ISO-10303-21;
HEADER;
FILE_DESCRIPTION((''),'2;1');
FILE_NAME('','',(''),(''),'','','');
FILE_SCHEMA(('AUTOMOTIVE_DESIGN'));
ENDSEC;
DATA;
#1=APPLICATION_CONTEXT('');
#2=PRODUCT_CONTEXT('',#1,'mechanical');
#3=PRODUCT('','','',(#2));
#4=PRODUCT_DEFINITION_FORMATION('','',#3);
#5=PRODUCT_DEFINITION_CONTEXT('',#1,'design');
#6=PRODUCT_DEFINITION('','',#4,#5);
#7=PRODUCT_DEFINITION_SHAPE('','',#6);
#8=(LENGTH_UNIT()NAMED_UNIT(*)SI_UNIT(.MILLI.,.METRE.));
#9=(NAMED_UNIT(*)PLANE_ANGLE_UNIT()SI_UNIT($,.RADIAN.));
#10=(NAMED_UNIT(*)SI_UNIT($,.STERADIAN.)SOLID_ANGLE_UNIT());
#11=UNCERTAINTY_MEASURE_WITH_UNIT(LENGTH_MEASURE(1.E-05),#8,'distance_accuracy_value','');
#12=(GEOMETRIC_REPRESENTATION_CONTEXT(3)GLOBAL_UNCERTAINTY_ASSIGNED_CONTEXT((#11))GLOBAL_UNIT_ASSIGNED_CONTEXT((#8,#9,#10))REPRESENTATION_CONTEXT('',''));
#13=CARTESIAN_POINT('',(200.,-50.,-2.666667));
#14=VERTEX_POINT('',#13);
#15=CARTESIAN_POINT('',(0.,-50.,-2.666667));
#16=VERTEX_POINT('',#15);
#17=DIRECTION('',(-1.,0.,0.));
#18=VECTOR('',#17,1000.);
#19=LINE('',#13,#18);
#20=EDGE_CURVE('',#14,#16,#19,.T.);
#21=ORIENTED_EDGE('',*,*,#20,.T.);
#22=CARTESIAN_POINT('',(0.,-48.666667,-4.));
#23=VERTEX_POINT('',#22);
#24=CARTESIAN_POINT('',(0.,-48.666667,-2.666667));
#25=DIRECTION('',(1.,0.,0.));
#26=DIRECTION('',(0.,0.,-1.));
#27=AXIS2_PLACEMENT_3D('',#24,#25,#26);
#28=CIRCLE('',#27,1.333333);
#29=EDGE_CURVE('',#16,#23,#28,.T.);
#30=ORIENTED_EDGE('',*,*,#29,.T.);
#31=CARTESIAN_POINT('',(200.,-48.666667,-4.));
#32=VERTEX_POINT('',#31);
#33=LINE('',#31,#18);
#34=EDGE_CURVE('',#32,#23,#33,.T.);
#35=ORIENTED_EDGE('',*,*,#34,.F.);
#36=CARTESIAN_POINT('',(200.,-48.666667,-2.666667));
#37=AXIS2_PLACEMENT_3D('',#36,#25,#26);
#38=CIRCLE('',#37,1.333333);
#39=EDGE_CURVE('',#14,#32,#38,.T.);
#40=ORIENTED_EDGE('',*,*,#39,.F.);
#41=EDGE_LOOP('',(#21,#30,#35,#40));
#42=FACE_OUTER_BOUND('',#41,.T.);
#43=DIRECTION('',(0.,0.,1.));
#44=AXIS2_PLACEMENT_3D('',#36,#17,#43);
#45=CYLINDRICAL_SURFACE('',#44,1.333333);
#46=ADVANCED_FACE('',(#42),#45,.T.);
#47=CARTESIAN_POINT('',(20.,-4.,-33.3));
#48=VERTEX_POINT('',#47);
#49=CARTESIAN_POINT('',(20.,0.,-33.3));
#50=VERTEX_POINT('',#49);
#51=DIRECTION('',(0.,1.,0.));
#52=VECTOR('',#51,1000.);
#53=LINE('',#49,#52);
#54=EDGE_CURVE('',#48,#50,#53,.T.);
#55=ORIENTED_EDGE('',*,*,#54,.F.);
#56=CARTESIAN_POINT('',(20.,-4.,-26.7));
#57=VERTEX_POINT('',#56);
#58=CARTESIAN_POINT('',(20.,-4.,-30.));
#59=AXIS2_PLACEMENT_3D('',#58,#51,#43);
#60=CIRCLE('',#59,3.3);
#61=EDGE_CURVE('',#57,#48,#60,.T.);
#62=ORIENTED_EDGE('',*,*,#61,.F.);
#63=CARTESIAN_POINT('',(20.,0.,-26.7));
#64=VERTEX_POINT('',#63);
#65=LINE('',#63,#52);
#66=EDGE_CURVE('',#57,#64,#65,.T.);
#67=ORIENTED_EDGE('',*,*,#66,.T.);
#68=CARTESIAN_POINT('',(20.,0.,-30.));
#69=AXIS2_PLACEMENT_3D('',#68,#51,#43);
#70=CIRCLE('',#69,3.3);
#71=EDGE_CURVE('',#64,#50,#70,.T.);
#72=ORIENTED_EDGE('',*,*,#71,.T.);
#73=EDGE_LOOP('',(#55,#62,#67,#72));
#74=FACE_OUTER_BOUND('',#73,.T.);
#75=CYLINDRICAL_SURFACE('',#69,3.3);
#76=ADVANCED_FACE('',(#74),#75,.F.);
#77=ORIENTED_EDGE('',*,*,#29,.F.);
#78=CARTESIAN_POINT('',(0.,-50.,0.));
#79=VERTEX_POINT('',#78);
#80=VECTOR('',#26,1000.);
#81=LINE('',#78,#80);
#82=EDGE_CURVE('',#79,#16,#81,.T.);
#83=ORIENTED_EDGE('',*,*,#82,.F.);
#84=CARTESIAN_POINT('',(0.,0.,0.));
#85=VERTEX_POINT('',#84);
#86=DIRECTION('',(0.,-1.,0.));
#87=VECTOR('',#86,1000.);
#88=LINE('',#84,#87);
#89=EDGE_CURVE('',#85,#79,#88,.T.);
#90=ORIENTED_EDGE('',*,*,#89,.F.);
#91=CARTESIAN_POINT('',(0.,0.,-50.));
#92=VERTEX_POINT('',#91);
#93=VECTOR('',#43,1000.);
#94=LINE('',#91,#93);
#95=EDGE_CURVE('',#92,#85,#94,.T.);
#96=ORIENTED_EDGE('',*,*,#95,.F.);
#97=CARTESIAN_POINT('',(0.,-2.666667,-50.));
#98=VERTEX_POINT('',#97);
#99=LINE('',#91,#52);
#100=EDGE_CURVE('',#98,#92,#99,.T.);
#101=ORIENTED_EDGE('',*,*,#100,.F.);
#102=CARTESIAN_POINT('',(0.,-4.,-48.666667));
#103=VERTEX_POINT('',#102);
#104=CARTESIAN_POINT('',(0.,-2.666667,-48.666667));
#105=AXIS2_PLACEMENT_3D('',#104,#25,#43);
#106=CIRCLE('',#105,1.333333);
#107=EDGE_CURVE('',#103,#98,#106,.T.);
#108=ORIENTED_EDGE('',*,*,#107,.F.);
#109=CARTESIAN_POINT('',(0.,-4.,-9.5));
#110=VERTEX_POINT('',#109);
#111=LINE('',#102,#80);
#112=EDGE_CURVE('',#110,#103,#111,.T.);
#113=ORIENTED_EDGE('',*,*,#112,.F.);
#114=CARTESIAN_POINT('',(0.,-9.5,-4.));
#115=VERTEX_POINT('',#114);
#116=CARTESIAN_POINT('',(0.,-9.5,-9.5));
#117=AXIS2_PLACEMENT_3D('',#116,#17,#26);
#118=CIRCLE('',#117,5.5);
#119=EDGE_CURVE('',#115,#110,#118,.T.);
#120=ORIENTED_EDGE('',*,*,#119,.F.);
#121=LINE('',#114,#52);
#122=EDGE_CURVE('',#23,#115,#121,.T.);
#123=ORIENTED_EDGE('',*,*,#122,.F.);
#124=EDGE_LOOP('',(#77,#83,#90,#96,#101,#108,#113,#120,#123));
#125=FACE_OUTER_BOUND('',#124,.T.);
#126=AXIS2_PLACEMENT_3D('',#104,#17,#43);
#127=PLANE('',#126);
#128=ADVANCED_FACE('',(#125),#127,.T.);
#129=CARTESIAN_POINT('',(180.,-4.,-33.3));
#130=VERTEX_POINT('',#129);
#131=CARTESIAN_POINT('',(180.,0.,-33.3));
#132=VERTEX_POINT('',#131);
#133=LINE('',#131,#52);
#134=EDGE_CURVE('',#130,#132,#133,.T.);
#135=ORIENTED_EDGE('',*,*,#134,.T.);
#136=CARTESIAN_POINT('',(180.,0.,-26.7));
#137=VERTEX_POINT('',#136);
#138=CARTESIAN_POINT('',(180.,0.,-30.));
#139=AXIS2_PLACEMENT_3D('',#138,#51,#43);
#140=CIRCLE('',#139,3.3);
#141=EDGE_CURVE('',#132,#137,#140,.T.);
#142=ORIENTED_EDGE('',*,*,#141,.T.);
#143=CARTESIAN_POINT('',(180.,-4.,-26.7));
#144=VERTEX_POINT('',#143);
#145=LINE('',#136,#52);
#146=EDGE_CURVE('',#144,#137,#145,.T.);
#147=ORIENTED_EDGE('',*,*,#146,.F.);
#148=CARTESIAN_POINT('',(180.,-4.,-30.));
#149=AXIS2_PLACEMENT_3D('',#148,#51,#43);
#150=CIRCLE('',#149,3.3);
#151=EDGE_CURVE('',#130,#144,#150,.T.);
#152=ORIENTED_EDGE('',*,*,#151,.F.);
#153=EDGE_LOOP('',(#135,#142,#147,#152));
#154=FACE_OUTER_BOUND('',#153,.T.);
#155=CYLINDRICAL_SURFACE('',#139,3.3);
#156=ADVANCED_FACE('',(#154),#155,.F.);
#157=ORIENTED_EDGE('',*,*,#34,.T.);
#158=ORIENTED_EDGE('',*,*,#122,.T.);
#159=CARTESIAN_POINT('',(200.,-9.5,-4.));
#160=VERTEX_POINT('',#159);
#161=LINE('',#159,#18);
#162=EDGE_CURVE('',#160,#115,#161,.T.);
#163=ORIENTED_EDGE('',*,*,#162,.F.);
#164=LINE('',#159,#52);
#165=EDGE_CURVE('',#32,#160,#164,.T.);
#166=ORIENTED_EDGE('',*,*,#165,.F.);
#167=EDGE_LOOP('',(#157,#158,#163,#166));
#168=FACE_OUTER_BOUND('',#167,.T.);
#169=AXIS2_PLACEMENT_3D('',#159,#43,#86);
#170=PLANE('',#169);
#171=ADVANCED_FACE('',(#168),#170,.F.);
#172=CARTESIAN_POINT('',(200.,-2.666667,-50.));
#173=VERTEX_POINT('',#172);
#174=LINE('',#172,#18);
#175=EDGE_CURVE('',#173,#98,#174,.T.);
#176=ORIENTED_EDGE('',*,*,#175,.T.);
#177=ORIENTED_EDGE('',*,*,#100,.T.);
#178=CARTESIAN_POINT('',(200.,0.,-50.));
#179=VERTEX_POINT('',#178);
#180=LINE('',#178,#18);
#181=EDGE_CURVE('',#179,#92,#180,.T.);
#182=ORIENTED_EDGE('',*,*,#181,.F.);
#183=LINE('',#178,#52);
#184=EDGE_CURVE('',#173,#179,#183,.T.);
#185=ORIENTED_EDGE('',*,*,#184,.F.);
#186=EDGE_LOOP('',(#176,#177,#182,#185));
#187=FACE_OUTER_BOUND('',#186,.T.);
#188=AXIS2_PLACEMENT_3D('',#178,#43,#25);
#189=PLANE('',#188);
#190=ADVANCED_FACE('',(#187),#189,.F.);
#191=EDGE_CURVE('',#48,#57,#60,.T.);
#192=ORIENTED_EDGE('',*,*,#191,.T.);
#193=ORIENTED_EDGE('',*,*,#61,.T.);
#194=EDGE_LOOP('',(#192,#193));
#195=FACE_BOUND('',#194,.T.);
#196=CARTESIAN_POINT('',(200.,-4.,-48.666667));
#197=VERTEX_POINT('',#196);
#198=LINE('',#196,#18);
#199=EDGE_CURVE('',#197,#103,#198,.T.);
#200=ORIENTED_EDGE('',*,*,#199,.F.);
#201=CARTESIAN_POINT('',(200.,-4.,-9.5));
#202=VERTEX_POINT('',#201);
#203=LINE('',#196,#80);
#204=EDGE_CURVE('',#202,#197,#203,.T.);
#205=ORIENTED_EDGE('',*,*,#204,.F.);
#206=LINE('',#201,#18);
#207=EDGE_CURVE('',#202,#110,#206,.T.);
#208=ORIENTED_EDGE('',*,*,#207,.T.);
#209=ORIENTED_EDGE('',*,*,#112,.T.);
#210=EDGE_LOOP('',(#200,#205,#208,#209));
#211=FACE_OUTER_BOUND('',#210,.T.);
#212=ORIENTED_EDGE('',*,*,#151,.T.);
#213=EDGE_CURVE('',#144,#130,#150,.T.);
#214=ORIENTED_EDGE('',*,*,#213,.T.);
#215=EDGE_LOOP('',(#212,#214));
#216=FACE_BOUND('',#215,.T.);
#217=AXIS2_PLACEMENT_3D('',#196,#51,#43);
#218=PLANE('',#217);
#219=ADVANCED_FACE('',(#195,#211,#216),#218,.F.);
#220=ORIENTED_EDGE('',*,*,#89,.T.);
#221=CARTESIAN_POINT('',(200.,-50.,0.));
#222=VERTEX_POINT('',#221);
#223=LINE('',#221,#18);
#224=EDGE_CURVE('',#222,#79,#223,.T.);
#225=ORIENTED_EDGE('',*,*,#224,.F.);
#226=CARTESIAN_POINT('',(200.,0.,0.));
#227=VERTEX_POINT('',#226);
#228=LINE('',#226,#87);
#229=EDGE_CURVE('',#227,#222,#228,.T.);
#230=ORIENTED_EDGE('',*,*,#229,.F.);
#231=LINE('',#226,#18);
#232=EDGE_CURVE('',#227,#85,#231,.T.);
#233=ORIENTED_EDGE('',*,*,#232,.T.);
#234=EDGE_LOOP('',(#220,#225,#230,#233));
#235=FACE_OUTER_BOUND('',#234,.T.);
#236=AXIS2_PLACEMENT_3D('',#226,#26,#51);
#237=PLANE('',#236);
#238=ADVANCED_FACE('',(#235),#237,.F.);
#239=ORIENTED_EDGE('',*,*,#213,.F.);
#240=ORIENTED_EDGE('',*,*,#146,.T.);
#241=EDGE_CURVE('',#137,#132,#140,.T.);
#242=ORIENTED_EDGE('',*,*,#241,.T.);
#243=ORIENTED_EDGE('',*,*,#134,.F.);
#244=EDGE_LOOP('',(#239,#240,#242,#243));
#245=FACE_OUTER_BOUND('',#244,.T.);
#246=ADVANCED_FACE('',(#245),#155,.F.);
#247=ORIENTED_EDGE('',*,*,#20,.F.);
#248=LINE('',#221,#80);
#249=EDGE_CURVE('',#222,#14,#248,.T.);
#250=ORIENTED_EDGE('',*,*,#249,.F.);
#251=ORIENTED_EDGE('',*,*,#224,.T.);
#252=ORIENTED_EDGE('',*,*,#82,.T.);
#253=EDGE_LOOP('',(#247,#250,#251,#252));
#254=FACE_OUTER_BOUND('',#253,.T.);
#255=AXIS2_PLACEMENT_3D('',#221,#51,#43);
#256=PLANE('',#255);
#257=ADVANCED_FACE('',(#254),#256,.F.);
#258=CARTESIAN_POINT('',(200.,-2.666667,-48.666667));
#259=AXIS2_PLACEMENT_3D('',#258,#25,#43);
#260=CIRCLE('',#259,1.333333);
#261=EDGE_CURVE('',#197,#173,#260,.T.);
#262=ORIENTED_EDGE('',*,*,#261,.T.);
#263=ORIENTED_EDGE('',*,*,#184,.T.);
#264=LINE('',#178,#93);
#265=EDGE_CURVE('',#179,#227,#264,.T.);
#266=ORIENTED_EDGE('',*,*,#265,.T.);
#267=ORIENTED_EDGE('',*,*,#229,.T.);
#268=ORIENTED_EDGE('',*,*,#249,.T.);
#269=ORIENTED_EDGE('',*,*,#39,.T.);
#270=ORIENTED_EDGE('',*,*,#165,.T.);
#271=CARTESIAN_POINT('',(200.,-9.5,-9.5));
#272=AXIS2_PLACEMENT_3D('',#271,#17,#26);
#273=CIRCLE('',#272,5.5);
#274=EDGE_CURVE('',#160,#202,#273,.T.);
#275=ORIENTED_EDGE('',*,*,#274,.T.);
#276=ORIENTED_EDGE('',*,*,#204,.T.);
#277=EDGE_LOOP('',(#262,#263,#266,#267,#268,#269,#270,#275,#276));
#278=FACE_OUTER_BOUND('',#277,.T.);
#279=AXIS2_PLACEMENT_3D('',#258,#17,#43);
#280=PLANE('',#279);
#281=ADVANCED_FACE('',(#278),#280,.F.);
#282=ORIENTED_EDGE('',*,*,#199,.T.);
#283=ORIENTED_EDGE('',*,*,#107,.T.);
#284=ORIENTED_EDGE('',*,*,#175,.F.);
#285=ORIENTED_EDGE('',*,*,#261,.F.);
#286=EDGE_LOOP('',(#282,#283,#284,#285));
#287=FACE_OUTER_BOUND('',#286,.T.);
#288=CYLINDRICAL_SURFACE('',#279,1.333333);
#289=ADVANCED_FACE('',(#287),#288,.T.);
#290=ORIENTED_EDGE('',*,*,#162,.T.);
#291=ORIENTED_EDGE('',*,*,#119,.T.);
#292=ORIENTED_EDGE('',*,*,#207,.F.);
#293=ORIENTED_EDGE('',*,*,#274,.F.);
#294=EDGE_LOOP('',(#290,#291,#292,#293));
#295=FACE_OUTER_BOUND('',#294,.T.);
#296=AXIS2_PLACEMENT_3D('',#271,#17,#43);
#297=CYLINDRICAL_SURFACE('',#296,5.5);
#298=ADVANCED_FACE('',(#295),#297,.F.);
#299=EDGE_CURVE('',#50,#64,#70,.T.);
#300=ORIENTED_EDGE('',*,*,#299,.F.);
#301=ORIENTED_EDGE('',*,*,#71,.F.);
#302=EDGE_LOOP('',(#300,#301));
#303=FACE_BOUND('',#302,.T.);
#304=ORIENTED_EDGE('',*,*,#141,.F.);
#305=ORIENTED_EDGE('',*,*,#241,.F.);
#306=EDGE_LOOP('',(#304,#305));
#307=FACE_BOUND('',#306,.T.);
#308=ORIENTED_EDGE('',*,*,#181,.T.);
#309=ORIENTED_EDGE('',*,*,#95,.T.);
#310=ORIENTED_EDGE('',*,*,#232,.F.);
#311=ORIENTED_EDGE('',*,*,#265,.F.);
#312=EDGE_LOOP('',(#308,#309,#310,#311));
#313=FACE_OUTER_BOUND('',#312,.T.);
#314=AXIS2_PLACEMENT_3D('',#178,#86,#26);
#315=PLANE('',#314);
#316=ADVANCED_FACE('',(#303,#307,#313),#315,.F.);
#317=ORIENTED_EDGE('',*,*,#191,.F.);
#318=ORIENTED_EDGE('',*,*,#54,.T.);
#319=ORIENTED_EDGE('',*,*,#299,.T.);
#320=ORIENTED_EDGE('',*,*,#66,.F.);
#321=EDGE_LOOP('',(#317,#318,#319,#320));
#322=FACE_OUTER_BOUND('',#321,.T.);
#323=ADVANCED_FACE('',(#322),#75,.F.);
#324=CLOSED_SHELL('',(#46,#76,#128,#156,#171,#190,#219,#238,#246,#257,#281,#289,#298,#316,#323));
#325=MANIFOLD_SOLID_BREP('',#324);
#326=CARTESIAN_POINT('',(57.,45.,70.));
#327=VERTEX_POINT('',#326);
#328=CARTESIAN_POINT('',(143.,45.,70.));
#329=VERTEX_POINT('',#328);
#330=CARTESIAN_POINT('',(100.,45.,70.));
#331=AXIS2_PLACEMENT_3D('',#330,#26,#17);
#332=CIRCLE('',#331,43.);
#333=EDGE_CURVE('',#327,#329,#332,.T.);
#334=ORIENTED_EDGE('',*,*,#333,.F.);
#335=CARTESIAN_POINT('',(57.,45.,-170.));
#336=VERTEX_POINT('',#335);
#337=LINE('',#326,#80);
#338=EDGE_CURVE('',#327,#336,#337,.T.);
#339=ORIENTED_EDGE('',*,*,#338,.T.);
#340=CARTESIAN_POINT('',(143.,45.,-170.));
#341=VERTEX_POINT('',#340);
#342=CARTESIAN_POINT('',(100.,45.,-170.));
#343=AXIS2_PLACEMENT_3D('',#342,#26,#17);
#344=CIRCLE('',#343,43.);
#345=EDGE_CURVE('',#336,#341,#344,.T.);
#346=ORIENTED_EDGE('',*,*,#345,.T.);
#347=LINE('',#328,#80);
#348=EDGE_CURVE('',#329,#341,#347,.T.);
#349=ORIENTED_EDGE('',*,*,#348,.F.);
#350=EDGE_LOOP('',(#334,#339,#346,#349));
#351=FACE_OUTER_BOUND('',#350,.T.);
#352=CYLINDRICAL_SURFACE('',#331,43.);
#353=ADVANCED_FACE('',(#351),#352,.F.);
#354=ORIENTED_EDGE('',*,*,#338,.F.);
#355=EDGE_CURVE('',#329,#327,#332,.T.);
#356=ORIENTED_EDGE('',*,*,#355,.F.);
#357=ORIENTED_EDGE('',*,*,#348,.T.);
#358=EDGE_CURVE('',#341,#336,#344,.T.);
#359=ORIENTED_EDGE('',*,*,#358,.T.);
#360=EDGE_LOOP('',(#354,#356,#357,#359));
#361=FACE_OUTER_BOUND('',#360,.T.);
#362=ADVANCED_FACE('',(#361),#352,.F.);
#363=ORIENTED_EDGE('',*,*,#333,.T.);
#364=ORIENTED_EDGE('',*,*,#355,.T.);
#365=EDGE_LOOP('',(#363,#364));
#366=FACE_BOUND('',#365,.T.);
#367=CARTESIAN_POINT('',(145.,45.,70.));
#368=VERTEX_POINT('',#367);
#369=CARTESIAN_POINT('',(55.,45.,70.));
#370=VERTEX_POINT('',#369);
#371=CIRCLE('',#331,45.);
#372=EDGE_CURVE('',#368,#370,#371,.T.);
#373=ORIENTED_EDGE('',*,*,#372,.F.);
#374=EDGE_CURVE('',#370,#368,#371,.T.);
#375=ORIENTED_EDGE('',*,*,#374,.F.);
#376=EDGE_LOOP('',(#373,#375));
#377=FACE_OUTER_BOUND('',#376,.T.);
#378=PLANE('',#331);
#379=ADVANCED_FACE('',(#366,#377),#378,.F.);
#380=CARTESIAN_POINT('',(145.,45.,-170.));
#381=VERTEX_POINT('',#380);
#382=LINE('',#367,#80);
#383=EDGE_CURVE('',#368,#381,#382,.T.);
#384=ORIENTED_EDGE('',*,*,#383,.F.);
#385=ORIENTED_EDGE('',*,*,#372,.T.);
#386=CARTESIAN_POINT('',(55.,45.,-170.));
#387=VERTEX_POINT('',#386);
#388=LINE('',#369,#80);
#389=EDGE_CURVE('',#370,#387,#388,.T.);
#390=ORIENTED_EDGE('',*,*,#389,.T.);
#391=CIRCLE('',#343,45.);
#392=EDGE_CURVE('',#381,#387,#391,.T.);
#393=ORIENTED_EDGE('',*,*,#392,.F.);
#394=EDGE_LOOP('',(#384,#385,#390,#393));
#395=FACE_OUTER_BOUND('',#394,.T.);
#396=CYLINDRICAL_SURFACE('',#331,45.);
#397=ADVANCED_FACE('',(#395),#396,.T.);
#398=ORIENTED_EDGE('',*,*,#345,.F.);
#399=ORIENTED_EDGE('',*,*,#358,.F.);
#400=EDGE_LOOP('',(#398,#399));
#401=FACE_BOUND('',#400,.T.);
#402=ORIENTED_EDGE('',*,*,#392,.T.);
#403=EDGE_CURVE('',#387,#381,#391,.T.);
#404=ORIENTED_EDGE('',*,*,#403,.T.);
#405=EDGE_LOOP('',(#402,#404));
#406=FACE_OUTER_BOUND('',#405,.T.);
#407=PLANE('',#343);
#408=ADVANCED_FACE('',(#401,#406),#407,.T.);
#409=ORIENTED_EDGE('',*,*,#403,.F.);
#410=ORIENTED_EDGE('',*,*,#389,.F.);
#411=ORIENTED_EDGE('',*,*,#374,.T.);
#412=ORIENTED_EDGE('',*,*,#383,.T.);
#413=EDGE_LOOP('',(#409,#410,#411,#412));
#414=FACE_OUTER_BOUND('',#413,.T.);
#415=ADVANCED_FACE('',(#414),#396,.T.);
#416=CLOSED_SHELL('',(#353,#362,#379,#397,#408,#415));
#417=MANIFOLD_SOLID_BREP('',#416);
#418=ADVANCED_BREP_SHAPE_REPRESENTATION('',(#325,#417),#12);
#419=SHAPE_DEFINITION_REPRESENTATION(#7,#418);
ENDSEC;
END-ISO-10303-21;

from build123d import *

# Parameters (mm, degrees)
EQUAL_ANGLE_STEEL_5X4_1_DEPTH = 200
BOSS_EXTRUDE1_START           = 120
SKETCH3_R                     = 45
SKETCH3_R_2                   = 43
BOSS_EXTRUDE1_DEPTH           = 240
M6_CLEARANCE_HOLE1_AT_2_COUNT = 2
M6_CLEARANCE_HOLE1_AT_2_PITCH = 160


with BuildPart() as part:
    # Sketch1 → Equal Angle Steel 5X4(1) (new body)
    with BuildSketch(Plane(origin=(0, 0, 0), x_dir=(0, 0, -1), z_dir=(1, 0, 0))):
        with BuildLine():
            Line((50, 0), (0, 0))
            Line((0, 0), (0, -50))
            Line((0, -50), (2.666666667, -50))
            ThreePointArc((2.666666667, -50), (3.609475708, -49.609475708), (4, -48.666666667))
            Line((4, -48.666666667), (4, -9.5))
            ThreePointArc((4, -9.5), (5.610912703, -5.610912703), (9.5, -4))
            Line((9.5, -4), (48.666666667, -4))
            ThreePointArc((48.666666667, -4), (49.609475708, -3.609475708), (50, -2.666666667))
            Line((50, -2.666666667), (50, 0))
        make_face()
    extrude(amount=EQUAL_ANGLE_STEEL_5X4_1_DEPTH)

    # Sketch6 → M6 Clearance Hole1 (revolve, cut)
    with BuildSketch(Plane(origin=(20, 0, -30), x_dir=(0, 0, 1), z_dir=(1, 0, 0))):
        Polygon((0, 0), (0, 21.982840043), (3.3, 20), (3.3, 0), align=None)
    m6_clearance_hole1 = revolve(axis=Axis((20, 6.35, -30), (0, -1, 0)), mode=Mode.SUBTRACT)

    # M6 Clearance Hole1 at 2: M6 Clearance Hole1 ×2
    with Locations(*[(i * M6_CLEARANCE_HOLE1_AT_2_PITCH, 0, 0) for i in range(1, M6_CLEARANCE_HOLE1_AT_2_COUNT)]):
        add(m6_clearance_hole1, mode=Mode.SUBTRACT)


with BuildPart() as body_2:
    # Sketch3 → Boss-Extrude1 (new body)
    with BuildSketch(Plane(origin=(0, 0, -50), x_dir=(-1, 0, 0), z_dir=(0, 0, -1)).offset(BOSS_EXTRUDE1_START)):
        with Locations((-100, 45)):
            Circle(SKETCH3_R)
        with Locations((-100, 45)):
            Circle(SKETCH3_R_2, mode=Mode.SUBTRACT)
    extrude(amount=-BOSS_EXTRUDE1_DEPTH)


solid = Compound([part.part, body_2.part])
